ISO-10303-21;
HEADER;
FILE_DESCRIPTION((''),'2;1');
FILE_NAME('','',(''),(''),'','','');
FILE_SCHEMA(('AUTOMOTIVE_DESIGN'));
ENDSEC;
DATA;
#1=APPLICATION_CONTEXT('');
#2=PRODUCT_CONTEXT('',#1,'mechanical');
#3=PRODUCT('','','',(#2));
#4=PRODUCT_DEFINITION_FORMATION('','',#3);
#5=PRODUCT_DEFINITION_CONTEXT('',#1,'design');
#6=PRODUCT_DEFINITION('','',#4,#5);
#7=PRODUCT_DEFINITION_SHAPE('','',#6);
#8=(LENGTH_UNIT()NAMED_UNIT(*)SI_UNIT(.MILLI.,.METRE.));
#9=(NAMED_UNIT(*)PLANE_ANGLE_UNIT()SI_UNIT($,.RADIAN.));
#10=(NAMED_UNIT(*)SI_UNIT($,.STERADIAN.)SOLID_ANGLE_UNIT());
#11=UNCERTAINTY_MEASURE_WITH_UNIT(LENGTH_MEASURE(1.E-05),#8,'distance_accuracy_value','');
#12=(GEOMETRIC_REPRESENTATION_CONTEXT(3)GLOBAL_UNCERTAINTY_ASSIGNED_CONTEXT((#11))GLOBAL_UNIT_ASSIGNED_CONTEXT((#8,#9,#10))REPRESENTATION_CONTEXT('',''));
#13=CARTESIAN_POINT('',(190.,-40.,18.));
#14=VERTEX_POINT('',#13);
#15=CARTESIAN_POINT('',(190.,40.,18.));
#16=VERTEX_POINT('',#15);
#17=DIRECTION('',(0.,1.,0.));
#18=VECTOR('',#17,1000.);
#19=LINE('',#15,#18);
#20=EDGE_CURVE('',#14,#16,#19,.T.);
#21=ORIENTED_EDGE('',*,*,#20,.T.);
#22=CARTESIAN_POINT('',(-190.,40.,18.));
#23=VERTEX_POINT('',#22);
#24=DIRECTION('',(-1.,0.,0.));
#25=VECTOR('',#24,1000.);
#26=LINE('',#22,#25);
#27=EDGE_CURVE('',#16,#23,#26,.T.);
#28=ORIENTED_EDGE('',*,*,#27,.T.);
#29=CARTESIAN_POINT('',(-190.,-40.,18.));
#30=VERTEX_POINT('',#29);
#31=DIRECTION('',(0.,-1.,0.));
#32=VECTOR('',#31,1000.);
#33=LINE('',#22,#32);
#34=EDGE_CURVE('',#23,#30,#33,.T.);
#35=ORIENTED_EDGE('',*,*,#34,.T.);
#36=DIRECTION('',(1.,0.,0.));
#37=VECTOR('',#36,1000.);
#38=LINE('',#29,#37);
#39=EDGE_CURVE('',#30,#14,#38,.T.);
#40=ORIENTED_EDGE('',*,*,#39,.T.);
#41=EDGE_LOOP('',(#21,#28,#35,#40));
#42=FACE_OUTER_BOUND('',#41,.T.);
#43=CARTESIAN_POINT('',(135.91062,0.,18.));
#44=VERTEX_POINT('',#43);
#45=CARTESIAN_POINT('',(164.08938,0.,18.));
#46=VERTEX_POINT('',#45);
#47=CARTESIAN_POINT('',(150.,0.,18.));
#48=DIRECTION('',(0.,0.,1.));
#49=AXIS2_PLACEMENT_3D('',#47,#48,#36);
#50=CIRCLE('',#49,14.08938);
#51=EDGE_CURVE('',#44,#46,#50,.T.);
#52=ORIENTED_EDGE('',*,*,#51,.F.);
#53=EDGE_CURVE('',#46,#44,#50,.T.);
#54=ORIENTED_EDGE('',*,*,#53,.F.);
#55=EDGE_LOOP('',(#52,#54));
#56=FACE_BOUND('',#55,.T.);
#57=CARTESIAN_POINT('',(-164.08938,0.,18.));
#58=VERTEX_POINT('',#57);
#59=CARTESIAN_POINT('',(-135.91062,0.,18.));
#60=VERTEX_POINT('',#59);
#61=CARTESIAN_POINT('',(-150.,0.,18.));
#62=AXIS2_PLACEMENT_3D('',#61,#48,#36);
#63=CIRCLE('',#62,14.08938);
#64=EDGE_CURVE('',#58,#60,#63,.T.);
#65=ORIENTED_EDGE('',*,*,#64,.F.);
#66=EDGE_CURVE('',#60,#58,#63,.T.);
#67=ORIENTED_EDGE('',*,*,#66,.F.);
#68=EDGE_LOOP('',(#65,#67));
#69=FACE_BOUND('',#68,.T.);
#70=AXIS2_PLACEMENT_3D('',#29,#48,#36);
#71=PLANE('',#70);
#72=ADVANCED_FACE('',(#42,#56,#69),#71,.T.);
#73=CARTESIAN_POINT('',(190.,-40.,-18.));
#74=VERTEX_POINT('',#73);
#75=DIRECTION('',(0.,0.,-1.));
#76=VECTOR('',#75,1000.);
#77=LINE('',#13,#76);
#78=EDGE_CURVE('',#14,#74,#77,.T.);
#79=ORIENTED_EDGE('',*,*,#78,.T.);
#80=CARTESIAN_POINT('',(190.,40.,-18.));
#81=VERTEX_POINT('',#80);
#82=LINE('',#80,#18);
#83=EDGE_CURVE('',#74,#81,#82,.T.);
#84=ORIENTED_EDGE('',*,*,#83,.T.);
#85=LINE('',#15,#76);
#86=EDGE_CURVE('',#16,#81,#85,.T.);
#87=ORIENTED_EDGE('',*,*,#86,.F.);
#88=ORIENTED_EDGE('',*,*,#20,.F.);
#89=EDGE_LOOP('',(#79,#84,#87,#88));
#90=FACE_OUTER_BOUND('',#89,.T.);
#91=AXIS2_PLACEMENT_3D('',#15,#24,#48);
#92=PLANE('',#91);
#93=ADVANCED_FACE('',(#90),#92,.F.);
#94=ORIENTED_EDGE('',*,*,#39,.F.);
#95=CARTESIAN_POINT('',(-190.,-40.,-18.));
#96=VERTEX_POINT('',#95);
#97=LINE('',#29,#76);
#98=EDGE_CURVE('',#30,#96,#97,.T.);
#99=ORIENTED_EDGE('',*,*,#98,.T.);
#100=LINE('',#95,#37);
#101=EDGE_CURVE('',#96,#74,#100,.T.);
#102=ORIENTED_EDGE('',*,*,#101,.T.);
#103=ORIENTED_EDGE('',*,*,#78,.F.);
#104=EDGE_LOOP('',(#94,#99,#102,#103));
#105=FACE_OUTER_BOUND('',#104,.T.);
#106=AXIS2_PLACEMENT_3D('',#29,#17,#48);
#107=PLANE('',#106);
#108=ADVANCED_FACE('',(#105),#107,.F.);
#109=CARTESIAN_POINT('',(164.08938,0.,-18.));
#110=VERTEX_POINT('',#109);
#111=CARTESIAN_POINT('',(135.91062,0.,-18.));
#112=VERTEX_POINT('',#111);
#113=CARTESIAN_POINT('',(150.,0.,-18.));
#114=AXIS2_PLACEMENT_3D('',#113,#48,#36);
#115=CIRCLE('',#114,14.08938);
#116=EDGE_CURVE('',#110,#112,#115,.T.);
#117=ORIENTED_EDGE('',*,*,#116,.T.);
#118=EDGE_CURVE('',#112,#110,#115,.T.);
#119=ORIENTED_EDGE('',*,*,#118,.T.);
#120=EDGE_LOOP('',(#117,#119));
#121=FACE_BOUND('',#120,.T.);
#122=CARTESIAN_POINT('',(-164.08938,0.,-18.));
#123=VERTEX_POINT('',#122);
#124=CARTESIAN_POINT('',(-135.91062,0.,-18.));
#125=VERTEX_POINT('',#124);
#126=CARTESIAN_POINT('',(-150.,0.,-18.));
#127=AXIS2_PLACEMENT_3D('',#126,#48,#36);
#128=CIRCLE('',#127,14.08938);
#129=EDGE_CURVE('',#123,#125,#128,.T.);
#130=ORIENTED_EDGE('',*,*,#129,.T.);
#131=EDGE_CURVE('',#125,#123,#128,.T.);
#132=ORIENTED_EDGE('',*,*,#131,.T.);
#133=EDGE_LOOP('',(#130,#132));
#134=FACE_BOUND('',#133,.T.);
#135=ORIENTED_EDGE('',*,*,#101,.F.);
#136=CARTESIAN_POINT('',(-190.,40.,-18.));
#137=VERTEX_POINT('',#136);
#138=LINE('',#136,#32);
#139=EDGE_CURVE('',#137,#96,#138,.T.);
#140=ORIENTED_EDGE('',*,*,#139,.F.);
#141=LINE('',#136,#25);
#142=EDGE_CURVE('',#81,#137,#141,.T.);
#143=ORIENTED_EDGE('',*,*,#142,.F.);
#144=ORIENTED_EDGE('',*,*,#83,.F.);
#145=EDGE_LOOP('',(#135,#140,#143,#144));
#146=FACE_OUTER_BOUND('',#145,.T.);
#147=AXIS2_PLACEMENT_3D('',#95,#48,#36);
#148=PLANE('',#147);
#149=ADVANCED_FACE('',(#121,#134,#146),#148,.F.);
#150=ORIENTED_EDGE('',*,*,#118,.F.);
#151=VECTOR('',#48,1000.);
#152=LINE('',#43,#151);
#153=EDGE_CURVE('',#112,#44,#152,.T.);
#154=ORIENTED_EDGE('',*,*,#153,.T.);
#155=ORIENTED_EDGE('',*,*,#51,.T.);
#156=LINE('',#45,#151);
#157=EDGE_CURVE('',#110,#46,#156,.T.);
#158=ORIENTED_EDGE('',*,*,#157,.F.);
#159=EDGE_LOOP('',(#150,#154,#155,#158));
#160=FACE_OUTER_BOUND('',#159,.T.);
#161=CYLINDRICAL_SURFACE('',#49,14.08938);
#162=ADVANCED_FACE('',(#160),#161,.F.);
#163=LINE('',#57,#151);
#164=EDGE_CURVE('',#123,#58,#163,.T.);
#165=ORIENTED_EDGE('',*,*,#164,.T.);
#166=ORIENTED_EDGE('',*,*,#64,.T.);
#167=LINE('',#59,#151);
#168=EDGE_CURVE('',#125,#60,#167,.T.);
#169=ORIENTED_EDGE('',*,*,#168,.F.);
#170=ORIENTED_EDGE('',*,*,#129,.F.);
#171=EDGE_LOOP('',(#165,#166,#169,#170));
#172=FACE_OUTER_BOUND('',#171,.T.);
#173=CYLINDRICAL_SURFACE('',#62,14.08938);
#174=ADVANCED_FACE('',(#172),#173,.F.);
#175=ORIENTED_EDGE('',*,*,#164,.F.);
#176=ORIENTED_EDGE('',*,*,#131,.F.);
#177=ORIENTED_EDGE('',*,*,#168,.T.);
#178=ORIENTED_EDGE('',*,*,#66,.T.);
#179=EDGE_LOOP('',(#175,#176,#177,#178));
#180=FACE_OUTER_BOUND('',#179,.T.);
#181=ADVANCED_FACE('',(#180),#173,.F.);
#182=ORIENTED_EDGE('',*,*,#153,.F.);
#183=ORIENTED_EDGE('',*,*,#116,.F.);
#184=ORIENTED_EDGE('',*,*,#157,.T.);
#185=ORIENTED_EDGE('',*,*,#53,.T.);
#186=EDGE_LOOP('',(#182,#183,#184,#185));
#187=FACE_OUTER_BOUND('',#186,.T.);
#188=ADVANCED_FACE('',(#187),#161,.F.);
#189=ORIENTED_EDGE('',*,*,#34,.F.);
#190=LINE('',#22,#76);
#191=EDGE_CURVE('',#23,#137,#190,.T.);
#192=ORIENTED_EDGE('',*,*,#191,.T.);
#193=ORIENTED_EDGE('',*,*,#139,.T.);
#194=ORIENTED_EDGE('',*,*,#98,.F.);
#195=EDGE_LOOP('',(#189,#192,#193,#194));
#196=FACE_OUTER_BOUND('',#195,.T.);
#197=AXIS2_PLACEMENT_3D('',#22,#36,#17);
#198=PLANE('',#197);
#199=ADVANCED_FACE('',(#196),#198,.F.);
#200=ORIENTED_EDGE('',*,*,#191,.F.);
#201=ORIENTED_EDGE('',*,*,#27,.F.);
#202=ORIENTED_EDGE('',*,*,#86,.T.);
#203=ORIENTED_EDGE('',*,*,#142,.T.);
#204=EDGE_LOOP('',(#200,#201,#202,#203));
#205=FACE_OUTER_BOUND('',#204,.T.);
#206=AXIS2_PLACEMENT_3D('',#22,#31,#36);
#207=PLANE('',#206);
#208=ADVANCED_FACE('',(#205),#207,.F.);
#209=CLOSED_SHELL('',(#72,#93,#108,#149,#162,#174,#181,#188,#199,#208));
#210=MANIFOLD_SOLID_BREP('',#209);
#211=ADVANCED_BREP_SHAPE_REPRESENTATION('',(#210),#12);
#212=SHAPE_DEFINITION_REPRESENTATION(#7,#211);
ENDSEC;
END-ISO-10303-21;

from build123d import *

# Parameters (mm, degrees)
SKETCH1_W                = 380
SKETCH1_H                = 80
BOSS_EXTRUDE1_DEPTH      = 18
F_1_1_4_7_TAPPED_HOLE1_D = 28.17876


with BuildPart() as part:
    # Sketch1 → Boss-Extrude1 (new, symmetric)
    with BuildSketch(Plane.XY):
        Rectangle(SKETCH1_W, SKETCH1_H)
    extrude(amount=BOSS_EXTRUDE1_DEPTH, both=True)

    # 1-1/4-7 Tapped Hole1 (through all)
    with Locations(Plane.XY.offset(18)):
        with Locations((-150, 0), (150, 0)):
            Hole(F_1_1_4_7_TAPPED_HOLE1_D / 2)


solid = part.part
